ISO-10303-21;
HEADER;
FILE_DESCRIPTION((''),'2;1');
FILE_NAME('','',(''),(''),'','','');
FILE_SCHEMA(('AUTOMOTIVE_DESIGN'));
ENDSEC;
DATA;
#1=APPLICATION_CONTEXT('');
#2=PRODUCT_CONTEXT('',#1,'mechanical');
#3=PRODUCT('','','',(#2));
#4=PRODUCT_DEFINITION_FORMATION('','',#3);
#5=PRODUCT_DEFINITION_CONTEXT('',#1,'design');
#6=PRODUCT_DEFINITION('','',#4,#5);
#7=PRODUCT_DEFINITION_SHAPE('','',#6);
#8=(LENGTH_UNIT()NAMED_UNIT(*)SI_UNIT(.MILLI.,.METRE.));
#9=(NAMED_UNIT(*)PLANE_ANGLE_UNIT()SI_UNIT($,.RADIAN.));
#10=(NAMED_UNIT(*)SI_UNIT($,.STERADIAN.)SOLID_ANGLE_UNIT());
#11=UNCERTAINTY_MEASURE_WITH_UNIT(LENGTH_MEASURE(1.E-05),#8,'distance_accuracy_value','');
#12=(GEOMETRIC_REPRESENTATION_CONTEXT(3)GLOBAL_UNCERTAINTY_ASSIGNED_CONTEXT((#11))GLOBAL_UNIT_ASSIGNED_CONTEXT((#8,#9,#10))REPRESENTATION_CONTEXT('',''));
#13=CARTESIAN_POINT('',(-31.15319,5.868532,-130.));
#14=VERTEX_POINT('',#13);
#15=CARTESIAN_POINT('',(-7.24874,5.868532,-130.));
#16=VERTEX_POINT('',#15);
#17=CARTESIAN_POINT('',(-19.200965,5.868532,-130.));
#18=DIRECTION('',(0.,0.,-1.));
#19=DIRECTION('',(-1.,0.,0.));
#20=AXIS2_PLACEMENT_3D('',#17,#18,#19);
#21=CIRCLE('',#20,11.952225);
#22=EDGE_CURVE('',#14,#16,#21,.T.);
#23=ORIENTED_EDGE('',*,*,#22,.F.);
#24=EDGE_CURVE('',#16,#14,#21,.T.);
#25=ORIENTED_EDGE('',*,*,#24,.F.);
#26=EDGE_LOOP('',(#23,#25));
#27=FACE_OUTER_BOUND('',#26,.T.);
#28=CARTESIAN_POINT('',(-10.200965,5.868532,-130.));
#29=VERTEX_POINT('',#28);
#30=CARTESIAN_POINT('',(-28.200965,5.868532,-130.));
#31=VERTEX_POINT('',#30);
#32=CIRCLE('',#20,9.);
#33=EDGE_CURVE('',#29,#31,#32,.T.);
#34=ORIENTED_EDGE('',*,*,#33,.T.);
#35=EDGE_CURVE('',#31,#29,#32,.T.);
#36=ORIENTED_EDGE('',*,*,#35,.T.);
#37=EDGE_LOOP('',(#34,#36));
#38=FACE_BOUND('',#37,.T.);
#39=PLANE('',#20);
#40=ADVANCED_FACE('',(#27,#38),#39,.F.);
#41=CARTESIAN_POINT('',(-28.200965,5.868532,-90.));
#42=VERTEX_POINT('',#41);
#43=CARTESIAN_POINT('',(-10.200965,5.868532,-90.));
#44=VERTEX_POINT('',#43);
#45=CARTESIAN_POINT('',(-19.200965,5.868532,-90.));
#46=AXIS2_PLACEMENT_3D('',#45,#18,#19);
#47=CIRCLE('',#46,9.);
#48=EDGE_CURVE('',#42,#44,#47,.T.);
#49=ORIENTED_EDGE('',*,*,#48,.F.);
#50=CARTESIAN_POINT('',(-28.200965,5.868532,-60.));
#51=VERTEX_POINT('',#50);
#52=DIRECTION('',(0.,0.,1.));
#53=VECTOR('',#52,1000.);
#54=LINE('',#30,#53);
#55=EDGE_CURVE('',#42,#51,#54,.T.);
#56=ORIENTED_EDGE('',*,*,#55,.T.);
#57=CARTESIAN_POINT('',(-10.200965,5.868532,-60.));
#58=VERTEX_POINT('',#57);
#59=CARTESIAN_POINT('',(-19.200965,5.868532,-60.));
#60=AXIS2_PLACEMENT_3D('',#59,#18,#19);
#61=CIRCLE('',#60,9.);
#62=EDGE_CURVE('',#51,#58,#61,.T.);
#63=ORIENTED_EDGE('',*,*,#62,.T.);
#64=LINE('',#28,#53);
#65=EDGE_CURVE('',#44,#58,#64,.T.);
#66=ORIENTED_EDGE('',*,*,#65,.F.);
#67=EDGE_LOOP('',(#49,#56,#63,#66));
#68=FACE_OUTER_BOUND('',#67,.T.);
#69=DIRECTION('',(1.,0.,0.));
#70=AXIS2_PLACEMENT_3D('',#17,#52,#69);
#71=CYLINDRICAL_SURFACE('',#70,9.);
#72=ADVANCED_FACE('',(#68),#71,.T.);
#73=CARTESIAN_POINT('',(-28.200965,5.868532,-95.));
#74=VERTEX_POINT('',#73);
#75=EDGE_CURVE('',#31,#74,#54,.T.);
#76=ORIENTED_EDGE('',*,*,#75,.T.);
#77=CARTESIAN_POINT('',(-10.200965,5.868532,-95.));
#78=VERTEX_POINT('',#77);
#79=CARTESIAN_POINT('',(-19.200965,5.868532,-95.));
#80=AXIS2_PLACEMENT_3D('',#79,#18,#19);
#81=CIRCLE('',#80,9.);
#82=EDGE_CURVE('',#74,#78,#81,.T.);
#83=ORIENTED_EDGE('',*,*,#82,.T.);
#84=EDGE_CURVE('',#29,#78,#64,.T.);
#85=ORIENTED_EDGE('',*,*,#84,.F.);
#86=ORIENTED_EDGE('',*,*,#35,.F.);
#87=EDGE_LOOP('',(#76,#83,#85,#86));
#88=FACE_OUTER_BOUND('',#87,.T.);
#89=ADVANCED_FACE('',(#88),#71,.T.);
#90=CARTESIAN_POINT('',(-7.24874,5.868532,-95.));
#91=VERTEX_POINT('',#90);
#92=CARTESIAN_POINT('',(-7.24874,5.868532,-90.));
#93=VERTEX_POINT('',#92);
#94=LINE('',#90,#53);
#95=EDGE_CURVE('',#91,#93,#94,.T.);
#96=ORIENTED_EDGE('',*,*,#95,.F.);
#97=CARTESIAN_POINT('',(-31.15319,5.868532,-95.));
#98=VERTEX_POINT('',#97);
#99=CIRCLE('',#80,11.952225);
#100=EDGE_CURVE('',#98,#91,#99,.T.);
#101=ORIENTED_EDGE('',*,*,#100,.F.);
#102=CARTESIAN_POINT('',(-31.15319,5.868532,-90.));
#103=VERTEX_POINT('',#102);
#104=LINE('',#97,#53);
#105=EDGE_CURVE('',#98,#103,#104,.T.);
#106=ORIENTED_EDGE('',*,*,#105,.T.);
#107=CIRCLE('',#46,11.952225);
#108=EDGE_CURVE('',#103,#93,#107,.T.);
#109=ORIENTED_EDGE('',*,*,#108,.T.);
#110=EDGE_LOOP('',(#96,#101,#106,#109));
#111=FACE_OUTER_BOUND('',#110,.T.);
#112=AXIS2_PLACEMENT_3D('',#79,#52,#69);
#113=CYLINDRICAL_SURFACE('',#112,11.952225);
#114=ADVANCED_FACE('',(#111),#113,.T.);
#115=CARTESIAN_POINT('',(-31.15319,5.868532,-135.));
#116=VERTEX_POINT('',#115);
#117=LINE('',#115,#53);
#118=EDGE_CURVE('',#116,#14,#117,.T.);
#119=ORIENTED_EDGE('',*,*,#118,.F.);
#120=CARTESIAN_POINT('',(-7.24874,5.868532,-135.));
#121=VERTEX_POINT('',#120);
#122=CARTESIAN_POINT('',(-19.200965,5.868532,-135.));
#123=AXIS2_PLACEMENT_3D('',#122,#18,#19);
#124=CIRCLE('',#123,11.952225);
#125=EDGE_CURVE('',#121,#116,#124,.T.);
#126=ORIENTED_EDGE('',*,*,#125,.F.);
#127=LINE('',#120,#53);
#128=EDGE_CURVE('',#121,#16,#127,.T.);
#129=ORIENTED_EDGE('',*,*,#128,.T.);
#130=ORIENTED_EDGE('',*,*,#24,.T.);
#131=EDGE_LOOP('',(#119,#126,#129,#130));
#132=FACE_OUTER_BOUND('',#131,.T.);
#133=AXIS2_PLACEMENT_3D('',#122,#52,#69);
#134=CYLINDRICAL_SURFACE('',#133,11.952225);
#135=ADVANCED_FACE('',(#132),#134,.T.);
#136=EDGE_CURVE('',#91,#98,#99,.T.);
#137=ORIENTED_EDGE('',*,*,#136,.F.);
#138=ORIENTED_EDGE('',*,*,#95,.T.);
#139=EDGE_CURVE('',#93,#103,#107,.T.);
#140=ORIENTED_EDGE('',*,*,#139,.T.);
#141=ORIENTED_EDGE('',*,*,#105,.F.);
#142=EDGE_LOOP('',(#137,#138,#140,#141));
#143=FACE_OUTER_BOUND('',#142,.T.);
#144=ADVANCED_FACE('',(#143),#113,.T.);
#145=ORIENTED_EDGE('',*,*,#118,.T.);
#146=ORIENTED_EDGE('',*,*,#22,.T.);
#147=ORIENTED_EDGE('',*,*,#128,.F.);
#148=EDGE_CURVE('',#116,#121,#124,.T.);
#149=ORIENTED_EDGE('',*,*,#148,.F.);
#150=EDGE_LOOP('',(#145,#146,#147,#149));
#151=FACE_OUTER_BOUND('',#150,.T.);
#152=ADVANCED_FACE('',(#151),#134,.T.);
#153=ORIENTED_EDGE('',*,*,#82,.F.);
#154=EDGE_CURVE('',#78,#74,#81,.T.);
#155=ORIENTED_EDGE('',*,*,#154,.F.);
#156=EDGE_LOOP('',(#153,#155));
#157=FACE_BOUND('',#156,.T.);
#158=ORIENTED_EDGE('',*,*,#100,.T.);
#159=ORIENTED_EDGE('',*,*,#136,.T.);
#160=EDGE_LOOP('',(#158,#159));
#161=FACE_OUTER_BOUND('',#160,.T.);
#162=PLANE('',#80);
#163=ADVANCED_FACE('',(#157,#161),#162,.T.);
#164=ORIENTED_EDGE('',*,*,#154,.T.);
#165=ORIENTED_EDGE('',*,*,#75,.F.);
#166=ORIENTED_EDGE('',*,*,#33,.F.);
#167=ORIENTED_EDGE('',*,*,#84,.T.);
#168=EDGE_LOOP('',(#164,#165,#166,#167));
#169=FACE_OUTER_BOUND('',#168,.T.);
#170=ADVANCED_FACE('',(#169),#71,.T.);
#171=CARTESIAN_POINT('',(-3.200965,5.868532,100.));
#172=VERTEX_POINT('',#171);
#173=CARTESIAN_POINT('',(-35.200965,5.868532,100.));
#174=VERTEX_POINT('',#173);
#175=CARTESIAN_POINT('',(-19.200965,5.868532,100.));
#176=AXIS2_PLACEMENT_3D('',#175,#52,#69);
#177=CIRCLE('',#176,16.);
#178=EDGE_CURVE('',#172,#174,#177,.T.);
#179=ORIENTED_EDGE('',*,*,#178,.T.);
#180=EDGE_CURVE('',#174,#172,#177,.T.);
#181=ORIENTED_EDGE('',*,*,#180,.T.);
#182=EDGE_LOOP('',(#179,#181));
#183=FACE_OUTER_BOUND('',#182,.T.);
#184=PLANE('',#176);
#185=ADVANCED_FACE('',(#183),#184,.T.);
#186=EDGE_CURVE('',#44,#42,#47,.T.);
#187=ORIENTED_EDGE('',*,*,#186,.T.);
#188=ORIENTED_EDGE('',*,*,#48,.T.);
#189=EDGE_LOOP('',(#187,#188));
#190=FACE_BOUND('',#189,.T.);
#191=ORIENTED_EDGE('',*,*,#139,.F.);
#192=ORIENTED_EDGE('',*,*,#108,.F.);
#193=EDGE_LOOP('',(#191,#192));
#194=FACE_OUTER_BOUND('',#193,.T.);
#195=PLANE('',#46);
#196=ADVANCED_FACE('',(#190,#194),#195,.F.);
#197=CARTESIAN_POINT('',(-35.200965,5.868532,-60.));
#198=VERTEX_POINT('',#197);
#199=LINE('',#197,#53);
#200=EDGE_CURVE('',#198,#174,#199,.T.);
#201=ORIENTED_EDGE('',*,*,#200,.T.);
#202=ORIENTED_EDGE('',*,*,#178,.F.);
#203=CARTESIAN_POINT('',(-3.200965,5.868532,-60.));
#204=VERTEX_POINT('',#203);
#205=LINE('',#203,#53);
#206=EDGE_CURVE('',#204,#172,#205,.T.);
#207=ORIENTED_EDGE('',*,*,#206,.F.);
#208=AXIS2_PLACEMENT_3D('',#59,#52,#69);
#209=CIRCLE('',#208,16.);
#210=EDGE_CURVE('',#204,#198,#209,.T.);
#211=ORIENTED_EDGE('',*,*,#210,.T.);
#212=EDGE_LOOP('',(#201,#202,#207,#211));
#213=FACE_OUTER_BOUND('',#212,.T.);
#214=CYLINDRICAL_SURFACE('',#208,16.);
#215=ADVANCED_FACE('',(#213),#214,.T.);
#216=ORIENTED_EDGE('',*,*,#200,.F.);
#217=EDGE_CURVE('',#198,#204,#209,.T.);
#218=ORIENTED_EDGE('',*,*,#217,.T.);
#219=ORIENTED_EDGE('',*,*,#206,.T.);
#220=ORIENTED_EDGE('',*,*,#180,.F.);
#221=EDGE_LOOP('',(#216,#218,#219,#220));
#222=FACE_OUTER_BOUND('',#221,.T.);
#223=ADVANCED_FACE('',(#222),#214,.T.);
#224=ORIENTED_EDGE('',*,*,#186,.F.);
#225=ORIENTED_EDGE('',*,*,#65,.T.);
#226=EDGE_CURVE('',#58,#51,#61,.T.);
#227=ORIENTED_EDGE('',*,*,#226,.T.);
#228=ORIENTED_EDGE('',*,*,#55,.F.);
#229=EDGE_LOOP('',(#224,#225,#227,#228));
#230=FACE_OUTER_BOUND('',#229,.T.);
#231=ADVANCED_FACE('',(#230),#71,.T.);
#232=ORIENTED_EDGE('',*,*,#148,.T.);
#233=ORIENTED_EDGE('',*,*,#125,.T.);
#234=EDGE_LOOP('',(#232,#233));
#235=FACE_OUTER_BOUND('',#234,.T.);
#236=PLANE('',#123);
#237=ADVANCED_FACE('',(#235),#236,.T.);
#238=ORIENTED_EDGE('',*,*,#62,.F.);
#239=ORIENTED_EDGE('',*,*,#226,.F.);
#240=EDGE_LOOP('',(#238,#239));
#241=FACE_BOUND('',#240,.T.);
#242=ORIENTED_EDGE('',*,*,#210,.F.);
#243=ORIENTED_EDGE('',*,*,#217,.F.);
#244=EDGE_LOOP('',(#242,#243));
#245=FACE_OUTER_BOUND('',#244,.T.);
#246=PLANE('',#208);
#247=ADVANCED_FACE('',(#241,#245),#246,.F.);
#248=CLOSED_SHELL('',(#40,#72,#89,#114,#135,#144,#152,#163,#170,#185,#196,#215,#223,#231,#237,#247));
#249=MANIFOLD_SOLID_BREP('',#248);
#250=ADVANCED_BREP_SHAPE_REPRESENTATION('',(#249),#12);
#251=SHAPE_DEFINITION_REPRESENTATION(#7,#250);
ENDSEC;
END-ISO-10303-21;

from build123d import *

# Parameters (mm, degrees)
SKETCH5_R           = 16
BOSS_EXTRUDE1_DEPTH = 60
SKETCH6_R           = 9
BOSS_EXTRUDE2_DEPTH = 70
BOSS_EXTRUDE3_START = 100
SKETCH7_R           = 16
BOSS_EXTRUDE3_DEPTH = 100
SKETCH8_R           = 11.952224842
BOSS_EXTRUDE4_DEPTH = 5
LPATTERN1_COUNT     = 2
LPATTERN1_PITCH     = 40


with BuildPart() as part:
    # Sketch5 → Boss-Extrude1 (new body)
    with BuildSketch(Plane.XY):
        with Locations((-19.20096517, 5.868531988)):
            Circle(SKETCH5_R)
    extrude(amount=-BOSS_EXTRUDE1_DEPTH)

    # Sketch6 → Boss-Extrude2 (add)
    with BuildSketch(Plane(origin=(0, 0, -60), x_dir=(-1, 0, 0), z_dir=(0, 0, -1))):
        with Locations((19.20096517, 5.868531988)):
            Circle(SKETCH6_R)
    extrude(amount=BOSS_EXTRUDE2_DEPTH)

    # Sketch7 → Boss-Extrude3 (add)
    with BuildSketch(Plane.XY.offset(BOSS_EXTRUDE3_START)):
        with Locations((-19.20096517, 5.868531988)):
            Circle(SKETCH7_R)
    extrude(amount=-BOSS_EXTRUDE3_DEPTH)

    # Sketch8 → Boss-Extrude4 (add)
    with BuildSketch(Plane(origin=(0, 0, -130), x_dir=(-1, 0, 0), z_dir=(0, 0, -1))):
        with Locations((19.20096517, 5.868531988)):
            Circle(SKETCH8_R)
    boss_extrude4 = extrude(amount=BOSS_EXTRUDE4_DEPTH)

    # LPattern1: Boss-Extrude4 ×2
    with Locations(*[(0, 0, i * LPATTERN1_PITCH) for i in range(1, LPATTERN1_COUNT)]):
        add(boss_extrude4)


solid = part.part
